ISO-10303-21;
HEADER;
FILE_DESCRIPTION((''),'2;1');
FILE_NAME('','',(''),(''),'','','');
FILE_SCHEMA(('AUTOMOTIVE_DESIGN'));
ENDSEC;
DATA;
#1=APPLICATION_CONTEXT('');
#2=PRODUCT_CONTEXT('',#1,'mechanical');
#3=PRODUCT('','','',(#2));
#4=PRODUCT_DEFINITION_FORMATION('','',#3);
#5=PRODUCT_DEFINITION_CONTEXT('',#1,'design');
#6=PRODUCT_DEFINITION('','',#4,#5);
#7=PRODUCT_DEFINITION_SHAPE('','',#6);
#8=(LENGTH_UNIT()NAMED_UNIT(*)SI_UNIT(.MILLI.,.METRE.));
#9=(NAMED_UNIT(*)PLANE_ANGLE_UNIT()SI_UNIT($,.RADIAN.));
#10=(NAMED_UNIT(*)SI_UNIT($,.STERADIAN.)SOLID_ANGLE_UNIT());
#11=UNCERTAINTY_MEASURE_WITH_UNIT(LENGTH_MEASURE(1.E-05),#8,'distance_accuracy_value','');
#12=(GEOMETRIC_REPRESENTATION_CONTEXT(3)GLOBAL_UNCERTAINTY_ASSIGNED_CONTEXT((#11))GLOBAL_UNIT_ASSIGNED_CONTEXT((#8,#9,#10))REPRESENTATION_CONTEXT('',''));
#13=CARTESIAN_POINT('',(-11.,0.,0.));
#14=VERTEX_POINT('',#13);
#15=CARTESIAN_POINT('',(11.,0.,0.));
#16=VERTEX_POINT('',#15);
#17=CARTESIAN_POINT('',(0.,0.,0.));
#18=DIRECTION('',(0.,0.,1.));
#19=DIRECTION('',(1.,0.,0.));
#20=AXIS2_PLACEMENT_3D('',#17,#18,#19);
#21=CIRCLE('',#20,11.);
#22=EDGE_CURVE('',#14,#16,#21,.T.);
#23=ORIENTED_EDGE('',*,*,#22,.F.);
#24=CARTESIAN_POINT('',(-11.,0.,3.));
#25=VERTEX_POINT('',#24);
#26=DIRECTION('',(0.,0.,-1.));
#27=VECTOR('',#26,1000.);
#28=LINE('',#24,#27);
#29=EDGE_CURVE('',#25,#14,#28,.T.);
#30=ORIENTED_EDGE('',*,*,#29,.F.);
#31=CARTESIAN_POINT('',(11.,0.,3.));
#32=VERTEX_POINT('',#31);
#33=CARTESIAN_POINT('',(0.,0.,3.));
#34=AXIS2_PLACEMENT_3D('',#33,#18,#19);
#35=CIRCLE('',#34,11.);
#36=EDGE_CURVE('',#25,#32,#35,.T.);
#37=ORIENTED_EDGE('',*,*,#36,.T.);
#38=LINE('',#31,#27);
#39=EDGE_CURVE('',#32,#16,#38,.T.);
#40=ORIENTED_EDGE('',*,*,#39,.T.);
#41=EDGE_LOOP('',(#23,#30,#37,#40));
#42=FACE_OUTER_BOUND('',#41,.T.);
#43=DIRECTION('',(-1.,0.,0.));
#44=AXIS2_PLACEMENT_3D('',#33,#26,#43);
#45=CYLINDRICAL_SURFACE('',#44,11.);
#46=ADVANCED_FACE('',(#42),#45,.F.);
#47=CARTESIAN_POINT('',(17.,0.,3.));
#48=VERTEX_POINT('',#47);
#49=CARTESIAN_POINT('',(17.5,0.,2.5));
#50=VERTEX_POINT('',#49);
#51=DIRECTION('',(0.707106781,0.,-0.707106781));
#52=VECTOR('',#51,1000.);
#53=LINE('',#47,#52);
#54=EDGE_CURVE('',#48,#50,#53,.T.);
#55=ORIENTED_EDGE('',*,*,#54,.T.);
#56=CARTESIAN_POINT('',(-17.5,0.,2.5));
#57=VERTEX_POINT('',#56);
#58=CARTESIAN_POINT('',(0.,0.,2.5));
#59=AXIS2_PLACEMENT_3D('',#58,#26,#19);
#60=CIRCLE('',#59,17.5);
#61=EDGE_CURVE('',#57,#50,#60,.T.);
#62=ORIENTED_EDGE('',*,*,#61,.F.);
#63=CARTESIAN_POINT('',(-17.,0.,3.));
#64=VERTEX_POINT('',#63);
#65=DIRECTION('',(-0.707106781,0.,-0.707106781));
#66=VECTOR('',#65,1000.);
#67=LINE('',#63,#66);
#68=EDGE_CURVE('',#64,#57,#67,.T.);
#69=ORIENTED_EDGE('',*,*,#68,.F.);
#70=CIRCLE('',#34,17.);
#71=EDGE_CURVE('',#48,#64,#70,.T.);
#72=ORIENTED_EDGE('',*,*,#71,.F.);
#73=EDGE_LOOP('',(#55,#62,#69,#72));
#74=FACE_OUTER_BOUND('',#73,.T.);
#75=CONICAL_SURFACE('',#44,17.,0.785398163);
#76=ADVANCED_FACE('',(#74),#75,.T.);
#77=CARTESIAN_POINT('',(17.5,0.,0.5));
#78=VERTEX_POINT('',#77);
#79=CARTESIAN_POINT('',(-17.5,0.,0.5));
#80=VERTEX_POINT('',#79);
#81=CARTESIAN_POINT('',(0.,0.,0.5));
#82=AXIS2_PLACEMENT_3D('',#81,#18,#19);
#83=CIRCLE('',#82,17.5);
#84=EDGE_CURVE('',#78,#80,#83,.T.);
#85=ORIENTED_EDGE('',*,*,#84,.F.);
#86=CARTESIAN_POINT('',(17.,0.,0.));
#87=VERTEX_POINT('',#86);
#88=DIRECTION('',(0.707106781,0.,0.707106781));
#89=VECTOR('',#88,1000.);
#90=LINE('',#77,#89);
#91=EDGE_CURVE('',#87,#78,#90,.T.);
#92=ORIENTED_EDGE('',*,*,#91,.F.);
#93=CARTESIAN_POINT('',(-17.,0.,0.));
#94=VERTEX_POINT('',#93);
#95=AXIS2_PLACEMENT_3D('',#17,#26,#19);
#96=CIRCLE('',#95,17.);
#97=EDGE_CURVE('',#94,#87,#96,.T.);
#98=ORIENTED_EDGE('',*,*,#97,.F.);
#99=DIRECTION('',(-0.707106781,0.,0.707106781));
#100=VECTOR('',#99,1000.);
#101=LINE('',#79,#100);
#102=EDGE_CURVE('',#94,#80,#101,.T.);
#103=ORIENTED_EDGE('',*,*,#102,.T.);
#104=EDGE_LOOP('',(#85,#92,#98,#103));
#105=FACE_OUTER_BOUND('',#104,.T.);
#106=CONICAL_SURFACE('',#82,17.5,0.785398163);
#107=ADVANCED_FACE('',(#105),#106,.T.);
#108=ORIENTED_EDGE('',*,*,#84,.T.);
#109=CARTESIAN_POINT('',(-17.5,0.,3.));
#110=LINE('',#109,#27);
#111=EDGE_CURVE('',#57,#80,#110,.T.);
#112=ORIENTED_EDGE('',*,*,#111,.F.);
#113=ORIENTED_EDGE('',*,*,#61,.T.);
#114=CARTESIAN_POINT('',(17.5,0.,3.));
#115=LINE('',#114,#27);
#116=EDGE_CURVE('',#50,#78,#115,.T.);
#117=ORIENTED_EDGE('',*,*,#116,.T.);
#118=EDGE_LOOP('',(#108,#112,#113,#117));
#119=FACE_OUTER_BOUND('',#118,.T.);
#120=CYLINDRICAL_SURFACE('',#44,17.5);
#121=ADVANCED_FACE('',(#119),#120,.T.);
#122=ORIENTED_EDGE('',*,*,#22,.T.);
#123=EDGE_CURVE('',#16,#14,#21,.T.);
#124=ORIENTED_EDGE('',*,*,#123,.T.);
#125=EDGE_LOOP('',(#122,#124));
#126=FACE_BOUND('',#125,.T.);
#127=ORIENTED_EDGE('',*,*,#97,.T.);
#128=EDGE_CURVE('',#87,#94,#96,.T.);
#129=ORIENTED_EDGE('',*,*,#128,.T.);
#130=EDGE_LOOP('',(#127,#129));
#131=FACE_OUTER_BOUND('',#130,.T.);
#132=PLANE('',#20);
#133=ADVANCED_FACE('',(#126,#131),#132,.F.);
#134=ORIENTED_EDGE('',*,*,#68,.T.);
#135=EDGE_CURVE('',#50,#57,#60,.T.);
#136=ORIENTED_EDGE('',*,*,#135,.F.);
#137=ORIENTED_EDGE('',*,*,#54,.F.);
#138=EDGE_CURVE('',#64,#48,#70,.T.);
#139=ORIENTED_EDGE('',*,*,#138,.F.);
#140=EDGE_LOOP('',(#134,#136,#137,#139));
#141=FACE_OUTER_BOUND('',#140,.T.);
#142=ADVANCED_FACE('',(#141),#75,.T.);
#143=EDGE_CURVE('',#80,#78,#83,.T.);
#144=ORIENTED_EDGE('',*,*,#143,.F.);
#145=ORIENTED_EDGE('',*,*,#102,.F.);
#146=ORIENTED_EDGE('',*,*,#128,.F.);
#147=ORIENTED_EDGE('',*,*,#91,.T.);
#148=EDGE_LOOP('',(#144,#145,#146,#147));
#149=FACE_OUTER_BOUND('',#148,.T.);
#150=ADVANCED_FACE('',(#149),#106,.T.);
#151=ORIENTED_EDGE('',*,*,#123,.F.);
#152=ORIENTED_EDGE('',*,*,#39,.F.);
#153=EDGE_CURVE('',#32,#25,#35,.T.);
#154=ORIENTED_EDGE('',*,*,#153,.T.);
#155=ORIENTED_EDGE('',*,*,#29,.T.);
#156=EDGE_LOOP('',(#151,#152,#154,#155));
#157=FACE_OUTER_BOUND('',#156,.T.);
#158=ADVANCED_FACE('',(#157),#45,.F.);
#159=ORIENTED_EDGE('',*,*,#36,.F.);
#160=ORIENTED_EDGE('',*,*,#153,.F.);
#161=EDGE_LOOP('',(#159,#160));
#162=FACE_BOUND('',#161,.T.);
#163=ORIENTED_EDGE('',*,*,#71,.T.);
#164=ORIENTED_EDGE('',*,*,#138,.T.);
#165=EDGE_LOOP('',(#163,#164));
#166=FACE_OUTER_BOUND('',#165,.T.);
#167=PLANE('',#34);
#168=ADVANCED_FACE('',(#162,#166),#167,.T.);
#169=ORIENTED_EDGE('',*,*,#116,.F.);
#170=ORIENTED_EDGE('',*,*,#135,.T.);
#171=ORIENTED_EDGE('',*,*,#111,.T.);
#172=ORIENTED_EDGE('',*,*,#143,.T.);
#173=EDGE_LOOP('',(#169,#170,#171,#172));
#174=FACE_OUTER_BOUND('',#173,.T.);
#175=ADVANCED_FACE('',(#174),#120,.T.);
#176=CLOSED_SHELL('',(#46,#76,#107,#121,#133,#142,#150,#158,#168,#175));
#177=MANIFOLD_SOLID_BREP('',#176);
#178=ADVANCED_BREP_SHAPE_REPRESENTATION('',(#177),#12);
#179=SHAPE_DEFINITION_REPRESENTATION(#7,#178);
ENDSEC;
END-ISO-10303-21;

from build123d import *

# Parameters (mm, degrees)
SKETCH_1_R      = 17.5
SKETCH_1_R_2    = 11
EXTRUDE_1_DEPTH = 3
CHAMFER_1_SIZE  = 0.5


with BuildPart() as part:
    # 草图1 → 拉伸1 (new body)
    with BuildSketch(Plane.XY):
        Circle(SKETCH_1_R)
        Circle(SKETCH_1_R_2, mode=Mode.SUBTRACT)
    extrude(amount=EXTRUDE_1_DEPTH)

    # 倒角1
    chamfer_1_edges = [part.edges().sort_by_distance(p)[0] for p in [
        (-17.5, 0, 0),
        (-17.5, 0, 3),
    ]]
    chamfer(chamfer_1_edges, length=CHAMFER_1_SIZE)


solid = part.part
